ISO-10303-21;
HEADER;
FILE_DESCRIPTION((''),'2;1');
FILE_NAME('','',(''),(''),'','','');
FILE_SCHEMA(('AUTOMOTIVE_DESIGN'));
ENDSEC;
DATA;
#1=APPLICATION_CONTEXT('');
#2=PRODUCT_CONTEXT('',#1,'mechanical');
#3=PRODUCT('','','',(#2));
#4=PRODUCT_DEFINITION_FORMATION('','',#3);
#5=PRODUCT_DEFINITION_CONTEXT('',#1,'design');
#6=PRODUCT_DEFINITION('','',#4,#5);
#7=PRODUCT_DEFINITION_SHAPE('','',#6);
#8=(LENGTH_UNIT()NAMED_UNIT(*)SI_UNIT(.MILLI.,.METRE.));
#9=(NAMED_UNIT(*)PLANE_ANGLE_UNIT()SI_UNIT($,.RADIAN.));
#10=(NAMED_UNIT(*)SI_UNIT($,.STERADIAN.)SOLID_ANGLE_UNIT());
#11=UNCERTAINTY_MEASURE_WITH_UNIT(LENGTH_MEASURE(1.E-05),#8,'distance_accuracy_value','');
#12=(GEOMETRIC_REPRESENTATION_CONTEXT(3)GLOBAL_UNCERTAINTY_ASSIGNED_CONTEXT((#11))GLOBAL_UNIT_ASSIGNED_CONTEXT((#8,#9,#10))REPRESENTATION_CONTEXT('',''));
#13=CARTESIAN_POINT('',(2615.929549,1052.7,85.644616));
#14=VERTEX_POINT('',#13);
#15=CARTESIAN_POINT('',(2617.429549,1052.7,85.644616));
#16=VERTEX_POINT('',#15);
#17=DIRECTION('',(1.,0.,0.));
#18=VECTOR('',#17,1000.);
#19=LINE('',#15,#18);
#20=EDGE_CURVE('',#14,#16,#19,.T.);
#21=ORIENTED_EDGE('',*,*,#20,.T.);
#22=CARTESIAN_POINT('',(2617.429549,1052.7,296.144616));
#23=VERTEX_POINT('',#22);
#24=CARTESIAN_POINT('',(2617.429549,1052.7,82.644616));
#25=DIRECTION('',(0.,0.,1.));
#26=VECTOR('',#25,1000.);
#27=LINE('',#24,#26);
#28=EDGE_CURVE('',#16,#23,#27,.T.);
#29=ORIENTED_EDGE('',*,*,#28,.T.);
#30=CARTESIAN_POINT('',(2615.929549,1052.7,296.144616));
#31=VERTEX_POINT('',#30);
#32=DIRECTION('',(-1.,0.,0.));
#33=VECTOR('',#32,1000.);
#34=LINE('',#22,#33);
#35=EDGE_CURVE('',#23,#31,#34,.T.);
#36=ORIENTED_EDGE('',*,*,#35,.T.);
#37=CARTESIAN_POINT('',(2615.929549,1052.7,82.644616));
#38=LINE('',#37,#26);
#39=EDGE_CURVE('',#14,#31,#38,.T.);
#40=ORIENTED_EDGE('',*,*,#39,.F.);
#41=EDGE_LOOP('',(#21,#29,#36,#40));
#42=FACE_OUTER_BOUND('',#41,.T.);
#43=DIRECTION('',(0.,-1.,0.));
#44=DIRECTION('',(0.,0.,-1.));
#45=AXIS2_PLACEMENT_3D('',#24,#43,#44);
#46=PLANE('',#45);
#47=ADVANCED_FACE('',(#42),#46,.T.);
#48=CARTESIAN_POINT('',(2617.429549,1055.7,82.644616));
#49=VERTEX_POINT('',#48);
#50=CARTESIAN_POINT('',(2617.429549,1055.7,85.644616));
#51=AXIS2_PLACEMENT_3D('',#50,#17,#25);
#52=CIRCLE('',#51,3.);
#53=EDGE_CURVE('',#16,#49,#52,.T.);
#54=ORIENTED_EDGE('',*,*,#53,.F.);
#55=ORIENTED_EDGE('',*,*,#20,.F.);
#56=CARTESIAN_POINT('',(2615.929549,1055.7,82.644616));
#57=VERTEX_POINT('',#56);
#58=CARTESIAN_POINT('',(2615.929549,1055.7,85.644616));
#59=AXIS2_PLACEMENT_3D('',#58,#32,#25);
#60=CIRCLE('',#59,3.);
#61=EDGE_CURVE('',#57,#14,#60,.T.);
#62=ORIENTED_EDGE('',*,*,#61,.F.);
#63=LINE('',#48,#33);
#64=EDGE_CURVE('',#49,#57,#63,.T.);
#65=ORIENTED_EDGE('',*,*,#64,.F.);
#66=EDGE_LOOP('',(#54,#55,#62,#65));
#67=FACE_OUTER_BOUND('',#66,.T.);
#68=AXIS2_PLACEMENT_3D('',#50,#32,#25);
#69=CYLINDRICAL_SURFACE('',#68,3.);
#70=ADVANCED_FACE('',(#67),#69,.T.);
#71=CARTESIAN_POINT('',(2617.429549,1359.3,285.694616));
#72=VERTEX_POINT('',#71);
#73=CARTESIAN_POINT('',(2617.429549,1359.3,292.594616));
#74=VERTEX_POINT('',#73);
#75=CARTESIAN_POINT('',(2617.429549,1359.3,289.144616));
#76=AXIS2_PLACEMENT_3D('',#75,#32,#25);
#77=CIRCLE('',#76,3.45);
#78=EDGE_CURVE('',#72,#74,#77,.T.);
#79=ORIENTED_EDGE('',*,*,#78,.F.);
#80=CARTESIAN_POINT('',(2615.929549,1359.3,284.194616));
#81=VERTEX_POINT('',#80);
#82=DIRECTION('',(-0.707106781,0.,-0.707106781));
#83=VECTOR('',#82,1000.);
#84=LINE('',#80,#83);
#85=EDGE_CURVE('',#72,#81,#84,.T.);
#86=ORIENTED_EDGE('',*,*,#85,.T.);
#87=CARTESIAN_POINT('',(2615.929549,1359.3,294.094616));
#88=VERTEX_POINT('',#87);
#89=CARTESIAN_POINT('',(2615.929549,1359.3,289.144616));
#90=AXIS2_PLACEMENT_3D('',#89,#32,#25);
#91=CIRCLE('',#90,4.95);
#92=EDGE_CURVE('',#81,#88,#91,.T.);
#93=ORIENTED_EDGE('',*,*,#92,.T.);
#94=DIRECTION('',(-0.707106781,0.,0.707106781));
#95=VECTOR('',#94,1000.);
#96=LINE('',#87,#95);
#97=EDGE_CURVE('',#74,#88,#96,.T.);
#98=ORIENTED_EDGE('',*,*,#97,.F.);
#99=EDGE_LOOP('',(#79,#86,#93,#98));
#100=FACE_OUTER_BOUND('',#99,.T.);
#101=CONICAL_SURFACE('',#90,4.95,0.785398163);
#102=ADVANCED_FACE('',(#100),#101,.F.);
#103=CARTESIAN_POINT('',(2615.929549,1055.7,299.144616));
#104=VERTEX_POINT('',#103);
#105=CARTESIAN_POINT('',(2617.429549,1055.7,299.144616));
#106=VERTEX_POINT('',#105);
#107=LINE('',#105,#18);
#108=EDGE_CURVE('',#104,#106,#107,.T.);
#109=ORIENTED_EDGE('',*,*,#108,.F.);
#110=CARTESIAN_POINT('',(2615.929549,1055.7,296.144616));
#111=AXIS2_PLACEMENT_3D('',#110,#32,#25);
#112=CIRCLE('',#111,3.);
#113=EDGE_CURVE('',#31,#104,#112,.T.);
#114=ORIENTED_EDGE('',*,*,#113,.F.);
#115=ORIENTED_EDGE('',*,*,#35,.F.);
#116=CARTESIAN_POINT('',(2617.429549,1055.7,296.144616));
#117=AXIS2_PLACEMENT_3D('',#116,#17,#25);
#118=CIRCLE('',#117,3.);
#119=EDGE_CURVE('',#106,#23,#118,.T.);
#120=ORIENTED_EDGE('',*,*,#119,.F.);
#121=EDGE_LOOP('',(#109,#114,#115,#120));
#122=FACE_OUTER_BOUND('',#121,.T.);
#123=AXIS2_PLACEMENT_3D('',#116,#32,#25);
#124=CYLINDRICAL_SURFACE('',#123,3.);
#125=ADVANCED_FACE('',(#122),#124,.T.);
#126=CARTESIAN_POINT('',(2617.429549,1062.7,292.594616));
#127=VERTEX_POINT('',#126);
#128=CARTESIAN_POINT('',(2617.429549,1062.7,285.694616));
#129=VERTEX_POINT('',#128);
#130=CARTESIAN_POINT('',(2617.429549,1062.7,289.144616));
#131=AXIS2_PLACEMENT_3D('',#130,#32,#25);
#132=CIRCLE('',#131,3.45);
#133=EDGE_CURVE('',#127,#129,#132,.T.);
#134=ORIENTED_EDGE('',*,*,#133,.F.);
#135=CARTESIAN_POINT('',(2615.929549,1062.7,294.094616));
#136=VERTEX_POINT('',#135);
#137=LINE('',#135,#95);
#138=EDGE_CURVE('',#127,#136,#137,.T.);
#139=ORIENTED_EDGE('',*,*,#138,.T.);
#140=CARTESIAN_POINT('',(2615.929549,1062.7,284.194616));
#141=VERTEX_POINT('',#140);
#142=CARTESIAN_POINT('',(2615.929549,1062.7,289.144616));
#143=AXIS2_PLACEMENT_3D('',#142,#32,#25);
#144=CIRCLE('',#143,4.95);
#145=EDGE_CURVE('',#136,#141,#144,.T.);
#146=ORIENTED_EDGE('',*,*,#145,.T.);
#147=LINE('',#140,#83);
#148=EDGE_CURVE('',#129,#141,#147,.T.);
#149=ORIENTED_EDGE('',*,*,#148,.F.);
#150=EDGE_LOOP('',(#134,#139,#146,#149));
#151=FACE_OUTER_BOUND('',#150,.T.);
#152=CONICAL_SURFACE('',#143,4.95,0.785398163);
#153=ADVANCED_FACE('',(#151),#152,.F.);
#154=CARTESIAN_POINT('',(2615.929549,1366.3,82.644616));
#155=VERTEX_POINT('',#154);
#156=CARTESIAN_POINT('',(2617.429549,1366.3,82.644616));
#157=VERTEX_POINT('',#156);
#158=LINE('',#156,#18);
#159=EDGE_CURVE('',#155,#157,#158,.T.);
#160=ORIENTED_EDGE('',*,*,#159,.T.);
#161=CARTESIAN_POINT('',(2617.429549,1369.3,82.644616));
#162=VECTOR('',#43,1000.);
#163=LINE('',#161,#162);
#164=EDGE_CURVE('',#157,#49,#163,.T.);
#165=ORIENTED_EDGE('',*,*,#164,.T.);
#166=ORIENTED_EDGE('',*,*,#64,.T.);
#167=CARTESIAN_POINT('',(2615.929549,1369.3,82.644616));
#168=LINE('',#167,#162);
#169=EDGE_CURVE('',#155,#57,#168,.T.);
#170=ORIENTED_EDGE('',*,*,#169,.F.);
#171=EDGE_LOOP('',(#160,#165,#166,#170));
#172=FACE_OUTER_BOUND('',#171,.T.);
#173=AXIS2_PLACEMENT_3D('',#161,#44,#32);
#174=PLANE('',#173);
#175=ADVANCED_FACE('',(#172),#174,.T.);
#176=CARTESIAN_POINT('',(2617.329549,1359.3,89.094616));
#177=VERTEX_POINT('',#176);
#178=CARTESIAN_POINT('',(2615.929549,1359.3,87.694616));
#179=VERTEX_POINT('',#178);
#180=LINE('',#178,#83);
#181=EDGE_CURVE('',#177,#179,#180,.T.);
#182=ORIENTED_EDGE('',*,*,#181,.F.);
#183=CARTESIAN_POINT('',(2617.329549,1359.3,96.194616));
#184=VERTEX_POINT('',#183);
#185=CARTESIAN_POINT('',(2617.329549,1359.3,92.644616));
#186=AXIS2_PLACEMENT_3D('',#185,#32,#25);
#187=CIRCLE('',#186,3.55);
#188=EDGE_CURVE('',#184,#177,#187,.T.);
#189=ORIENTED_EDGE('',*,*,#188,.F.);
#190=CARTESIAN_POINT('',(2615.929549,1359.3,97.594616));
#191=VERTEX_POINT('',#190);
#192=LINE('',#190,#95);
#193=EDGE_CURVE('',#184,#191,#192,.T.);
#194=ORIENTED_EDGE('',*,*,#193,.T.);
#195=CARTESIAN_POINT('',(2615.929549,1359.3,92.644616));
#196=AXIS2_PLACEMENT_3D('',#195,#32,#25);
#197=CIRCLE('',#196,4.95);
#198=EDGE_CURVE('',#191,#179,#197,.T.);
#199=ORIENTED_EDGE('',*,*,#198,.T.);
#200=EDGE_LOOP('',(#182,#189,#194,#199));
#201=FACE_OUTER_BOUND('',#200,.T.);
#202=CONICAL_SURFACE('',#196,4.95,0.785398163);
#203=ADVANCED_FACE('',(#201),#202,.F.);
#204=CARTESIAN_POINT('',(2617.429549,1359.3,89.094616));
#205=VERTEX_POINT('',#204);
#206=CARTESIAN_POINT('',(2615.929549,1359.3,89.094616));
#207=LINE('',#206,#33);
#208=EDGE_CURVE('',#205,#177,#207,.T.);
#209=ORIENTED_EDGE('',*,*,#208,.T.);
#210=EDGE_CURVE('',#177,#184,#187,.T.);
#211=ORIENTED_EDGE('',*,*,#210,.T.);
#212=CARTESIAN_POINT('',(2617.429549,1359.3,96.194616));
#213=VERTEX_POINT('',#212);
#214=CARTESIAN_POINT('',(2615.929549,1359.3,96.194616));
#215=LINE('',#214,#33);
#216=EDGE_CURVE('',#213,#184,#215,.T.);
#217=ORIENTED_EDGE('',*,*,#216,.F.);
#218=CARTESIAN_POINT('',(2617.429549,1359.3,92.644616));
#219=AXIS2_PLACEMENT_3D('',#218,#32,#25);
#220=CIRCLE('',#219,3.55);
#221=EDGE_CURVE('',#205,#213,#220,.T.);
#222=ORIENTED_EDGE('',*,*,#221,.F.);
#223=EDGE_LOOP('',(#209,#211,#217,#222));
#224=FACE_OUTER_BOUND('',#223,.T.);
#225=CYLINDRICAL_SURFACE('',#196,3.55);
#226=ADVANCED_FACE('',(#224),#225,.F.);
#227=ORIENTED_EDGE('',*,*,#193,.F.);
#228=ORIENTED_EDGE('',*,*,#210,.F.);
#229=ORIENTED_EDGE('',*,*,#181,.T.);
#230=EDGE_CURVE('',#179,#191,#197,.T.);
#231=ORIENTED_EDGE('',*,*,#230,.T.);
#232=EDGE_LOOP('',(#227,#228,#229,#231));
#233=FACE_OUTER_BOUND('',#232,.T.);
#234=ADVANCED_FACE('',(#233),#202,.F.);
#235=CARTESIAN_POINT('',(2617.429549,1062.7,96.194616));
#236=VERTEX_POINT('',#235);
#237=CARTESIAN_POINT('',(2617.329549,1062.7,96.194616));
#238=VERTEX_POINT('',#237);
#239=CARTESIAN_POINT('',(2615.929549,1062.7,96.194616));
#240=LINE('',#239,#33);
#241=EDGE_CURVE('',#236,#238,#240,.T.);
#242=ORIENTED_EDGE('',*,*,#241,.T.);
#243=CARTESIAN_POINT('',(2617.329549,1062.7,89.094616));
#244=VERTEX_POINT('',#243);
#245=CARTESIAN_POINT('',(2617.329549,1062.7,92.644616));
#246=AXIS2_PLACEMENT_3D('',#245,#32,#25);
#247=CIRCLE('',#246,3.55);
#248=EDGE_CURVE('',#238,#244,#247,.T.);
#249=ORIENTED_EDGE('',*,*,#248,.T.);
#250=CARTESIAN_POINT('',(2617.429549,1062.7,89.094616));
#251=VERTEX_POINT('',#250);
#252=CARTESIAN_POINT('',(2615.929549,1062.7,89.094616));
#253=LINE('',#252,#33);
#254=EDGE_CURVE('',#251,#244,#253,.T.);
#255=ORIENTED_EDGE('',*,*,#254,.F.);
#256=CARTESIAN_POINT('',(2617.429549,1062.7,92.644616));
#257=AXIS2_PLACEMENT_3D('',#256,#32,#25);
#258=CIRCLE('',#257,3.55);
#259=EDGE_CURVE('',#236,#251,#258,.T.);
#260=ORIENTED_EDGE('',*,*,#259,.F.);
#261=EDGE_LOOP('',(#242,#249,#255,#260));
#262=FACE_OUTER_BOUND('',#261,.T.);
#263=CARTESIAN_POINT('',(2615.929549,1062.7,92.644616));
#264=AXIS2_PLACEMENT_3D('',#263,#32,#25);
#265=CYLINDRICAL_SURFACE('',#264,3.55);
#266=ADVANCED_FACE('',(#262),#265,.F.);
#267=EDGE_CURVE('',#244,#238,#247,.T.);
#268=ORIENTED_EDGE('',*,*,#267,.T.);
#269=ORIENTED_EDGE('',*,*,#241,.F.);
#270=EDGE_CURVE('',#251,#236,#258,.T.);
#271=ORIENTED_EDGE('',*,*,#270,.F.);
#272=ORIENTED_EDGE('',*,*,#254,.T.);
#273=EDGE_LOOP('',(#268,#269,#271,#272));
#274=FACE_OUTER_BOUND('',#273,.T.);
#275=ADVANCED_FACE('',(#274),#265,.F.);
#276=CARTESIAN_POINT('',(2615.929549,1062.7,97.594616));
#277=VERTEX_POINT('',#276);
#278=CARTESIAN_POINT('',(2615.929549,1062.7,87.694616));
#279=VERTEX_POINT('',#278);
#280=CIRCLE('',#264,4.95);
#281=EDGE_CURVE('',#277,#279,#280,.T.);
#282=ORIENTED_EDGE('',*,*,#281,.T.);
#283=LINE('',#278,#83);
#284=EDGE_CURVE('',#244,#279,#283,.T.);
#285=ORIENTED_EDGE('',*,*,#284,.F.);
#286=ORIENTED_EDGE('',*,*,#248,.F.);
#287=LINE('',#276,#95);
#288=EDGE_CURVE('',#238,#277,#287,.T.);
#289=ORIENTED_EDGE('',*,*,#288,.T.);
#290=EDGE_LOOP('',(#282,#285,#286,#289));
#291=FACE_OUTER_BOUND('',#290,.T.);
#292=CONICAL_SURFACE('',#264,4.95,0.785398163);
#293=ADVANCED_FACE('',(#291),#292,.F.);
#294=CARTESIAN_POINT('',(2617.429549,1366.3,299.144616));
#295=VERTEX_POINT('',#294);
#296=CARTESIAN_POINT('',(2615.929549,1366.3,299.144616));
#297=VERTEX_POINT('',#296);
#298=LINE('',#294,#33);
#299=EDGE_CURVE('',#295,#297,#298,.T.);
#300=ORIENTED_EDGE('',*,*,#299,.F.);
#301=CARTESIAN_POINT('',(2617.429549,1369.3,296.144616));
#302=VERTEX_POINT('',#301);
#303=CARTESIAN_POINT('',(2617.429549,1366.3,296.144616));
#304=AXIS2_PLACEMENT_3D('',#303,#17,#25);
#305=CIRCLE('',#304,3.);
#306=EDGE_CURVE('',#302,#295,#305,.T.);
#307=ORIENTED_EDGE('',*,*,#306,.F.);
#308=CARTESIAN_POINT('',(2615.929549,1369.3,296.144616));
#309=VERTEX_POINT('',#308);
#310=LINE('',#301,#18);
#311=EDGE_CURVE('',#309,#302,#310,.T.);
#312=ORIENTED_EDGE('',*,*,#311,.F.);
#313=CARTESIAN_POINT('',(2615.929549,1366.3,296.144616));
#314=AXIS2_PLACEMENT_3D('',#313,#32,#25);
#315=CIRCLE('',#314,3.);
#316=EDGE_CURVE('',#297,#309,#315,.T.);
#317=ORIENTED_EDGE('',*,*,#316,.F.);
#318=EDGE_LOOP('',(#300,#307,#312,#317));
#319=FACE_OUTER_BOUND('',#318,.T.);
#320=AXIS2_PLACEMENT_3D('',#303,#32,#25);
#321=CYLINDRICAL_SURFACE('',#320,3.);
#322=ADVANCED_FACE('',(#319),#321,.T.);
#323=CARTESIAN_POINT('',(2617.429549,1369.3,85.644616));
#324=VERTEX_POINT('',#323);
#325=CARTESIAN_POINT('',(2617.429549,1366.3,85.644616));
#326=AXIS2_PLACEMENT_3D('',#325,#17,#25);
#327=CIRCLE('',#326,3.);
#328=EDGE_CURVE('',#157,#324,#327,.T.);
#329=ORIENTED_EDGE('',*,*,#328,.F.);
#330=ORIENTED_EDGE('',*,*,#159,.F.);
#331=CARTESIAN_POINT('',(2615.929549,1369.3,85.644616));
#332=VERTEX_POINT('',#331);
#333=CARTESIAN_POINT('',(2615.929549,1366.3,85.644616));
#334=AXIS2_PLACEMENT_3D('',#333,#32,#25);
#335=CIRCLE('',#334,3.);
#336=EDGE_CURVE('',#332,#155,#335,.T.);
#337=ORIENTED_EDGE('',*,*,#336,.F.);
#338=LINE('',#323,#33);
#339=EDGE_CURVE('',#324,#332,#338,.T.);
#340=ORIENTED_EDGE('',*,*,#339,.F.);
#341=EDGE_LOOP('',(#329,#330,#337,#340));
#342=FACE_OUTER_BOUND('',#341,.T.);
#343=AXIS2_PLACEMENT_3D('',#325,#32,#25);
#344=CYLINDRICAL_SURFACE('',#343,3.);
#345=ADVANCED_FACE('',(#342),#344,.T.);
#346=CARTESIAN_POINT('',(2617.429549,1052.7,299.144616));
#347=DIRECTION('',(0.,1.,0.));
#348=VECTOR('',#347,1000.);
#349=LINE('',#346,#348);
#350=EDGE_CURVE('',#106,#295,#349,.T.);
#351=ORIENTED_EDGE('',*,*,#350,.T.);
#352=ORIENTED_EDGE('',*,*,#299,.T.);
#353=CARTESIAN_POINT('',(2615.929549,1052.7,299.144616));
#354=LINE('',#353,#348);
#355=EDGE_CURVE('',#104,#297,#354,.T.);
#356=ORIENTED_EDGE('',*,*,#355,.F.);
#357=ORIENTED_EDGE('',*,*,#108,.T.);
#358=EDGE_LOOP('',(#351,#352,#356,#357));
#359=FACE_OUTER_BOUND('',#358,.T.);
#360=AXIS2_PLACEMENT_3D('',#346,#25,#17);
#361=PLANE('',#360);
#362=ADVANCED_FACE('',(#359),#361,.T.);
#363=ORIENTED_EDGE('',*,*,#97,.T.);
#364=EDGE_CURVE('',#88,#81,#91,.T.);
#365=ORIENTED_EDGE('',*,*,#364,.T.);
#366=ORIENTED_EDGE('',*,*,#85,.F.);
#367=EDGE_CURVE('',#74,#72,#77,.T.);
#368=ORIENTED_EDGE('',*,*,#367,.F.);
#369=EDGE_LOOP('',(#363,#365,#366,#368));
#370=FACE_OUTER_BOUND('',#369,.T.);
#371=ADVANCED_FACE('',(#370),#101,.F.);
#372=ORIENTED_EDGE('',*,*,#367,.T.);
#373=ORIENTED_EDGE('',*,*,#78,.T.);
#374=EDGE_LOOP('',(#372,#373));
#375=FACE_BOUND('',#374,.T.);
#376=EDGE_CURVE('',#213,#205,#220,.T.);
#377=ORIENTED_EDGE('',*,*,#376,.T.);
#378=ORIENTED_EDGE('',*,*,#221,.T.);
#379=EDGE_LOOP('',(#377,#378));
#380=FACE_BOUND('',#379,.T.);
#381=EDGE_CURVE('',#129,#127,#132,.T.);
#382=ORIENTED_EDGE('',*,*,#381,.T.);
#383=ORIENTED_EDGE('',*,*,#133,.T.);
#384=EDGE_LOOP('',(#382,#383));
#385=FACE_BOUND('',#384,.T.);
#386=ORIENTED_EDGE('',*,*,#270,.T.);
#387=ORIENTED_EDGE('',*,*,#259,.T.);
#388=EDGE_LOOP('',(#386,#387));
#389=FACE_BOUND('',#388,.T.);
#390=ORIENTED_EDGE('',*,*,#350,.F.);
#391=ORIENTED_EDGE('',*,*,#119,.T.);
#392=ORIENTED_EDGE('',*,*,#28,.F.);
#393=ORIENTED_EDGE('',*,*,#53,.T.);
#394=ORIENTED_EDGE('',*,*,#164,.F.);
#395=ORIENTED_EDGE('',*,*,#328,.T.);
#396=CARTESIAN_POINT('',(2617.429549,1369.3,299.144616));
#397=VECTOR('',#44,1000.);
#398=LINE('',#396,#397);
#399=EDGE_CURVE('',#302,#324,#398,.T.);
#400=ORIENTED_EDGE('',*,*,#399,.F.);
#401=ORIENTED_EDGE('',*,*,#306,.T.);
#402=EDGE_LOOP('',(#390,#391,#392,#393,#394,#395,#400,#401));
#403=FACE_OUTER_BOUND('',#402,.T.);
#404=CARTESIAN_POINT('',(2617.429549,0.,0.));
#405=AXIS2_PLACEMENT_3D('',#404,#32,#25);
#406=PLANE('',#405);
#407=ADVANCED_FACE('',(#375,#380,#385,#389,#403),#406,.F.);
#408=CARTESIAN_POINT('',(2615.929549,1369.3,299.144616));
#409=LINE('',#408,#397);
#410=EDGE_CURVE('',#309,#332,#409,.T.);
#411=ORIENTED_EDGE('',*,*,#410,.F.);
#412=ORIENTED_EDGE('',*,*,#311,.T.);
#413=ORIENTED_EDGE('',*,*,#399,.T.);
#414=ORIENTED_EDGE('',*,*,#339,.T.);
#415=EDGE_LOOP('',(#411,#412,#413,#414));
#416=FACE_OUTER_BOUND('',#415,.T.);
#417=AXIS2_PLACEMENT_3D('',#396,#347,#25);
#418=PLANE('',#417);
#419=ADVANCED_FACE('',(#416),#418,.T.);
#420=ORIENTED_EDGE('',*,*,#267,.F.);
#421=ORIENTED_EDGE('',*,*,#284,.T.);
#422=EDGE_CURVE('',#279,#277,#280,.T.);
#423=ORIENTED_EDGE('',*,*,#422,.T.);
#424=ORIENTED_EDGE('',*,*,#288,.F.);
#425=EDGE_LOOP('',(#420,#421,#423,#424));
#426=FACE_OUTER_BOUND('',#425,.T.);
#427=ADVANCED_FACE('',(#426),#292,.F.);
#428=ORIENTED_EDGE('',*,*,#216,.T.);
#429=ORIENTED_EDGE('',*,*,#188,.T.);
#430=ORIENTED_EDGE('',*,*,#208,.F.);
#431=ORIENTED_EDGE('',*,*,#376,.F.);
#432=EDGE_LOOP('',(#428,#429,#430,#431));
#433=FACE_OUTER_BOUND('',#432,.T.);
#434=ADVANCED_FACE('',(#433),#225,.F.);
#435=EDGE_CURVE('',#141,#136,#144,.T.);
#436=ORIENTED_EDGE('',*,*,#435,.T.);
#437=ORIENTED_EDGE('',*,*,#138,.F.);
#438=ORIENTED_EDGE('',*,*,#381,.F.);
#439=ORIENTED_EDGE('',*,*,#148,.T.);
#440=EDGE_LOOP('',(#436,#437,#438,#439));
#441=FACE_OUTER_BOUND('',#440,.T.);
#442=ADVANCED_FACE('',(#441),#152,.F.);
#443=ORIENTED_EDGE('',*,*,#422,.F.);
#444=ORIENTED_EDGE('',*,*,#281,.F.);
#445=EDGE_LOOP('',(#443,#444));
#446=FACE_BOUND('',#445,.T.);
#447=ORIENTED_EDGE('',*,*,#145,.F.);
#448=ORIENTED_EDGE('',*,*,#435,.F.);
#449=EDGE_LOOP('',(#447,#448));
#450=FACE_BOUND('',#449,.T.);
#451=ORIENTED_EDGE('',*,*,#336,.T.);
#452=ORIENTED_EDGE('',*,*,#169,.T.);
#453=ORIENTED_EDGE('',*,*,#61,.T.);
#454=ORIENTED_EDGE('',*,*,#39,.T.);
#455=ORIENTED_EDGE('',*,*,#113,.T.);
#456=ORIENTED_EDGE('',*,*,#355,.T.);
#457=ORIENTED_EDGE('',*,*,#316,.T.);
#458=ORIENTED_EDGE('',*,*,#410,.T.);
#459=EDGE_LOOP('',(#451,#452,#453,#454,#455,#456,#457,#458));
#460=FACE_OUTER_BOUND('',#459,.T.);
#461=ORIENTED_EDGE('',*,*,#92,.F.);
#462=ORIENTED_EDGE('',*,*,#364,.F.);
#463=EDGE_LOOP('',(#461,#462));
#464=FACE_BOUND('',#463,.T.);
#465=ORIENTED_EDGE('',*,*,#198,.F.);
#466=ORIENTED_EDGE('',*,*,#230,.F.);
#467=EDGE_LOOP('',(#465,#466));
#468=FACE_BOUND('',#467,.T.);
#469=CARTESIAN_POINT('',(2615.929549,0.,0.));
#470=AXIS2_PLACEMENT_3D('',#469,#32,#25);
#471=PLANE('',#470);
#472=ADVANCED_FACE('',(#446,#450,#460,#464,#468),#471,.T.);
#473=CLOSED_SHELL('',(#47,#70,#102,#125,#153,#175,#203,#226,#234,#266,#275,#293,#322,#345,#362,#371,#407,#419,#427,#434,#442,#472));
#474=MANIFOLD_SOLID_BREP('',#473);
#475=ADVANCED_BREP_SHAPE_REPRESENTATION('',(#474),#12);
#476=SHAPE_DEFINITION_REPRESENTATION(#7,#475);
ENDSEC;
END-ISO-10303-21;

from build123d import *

# Parameters (mm, degrees)
SKETCH_1_W                       = 316.6
SKETCH_1_H                       = 216.5
EXTRUDE_1_DEPTH                  = 1.5
HOLE_WIZARD_1_AT_2_COUNT         = 2
HOLE_WIZARD_1_AT_2_PITCH         = 296.6
HOLE_WIZARD_7_1_7_1_1_AT_2_COUNT = 2
HOLE_WIZARD_7_1_7_1_1_AT_2_PITCH = 296.6
FILLET_1_R                       = 3


with BuildPart() as part:
    # 草图1 → 凸台-拉伸1 (new body)
    with BuildSketch(Plane(origin=(2615.929548806, 0, 0), x_dir=(0, -1, 0), z_dir=(-1, 0, 0))):
        with Locations((-1211, 190.894615796)):
            Rectangle(SKETCH_1_W, SKETCH_1_H)
    extrude(amount=-EXTRUDE_1_DEPTH)

    # 草图2 → 孔1 (revolve, cut)
    with BuildSketch(Plane(origin=(2615.929548806, 1062.7, 289.144615796), x_dir=(0, 0, 1), z_dir=(0, 1, 0))):
        Polygon((0, 0), (0, 1.5), (3.45, 1.5), (4.95, 0), align=None)
    hole_wizard_1 = revolve(axis=Axis((2725.929548806, 1062.7, 289.144615796), (-1, 0, 0)), mode=Mode.SUBTRACT)

    # 孔1 at 2: 孔1 ×2
    with Locations(*[(0, i * HOLE_WIZARD_1_AT_2_PITCH, 0) for i in range(1, HOLE_WIZARD_1_AT_2_COUNT)]):
        add(hole_wizard_1, mode=Mode.SUBTRACT)

    # 草图4 → Ø7.1 (7.1) 直径孔1 (revolve, cut)
    with BuildSketch(Plane(origin=(2615.929548806, 1359.3, 92.644615796), x_dir=(0, 0, 1), z_dir=(0, 1, 0))):
        Polygon((0, 0), (0, 1.5), (3.55, 1.5), (3.55, 1.4), (4.95, 0), align=None)
    hole_wizard_7_1_7_1_1 = revolve(axis=Axis((2609.579548806, 1359.3, 92.644615796), (1, 0, 0)), mode=Mode.SUBTRACT)

    # Ø7.1 (7.1) 直径孔1 at 2: Ø7.1 (7.1) 直径孔1 ×2
    with Locations(*[(0, -i * HOLE_WIZARD_7_1_7_1_1_AT_2_PITCH, 0) for i in range(1, HOLE_WIZARD_7_1_7_1_1_AT_2_COUNT)]):
        add(hole_wizard_7_1_7_1_1, mode=Mode.SUBTRACT)

    # 圆角1
    fillet_1_edges = [part.edges().sort_by_distance(p)[0] for p in [
        (2616.679548806, 1052.7, 299.144615796),
        (2616.679548806, 1052.7, 82.644615796),
        (2616.679548806, 1369.3, 82.644615796),
        (2616.679548806, 1369.3, 299.144615796),
    ]]
    fillet(fillet_1_edges, radius=FILLET_1_R)


solid = part.part
